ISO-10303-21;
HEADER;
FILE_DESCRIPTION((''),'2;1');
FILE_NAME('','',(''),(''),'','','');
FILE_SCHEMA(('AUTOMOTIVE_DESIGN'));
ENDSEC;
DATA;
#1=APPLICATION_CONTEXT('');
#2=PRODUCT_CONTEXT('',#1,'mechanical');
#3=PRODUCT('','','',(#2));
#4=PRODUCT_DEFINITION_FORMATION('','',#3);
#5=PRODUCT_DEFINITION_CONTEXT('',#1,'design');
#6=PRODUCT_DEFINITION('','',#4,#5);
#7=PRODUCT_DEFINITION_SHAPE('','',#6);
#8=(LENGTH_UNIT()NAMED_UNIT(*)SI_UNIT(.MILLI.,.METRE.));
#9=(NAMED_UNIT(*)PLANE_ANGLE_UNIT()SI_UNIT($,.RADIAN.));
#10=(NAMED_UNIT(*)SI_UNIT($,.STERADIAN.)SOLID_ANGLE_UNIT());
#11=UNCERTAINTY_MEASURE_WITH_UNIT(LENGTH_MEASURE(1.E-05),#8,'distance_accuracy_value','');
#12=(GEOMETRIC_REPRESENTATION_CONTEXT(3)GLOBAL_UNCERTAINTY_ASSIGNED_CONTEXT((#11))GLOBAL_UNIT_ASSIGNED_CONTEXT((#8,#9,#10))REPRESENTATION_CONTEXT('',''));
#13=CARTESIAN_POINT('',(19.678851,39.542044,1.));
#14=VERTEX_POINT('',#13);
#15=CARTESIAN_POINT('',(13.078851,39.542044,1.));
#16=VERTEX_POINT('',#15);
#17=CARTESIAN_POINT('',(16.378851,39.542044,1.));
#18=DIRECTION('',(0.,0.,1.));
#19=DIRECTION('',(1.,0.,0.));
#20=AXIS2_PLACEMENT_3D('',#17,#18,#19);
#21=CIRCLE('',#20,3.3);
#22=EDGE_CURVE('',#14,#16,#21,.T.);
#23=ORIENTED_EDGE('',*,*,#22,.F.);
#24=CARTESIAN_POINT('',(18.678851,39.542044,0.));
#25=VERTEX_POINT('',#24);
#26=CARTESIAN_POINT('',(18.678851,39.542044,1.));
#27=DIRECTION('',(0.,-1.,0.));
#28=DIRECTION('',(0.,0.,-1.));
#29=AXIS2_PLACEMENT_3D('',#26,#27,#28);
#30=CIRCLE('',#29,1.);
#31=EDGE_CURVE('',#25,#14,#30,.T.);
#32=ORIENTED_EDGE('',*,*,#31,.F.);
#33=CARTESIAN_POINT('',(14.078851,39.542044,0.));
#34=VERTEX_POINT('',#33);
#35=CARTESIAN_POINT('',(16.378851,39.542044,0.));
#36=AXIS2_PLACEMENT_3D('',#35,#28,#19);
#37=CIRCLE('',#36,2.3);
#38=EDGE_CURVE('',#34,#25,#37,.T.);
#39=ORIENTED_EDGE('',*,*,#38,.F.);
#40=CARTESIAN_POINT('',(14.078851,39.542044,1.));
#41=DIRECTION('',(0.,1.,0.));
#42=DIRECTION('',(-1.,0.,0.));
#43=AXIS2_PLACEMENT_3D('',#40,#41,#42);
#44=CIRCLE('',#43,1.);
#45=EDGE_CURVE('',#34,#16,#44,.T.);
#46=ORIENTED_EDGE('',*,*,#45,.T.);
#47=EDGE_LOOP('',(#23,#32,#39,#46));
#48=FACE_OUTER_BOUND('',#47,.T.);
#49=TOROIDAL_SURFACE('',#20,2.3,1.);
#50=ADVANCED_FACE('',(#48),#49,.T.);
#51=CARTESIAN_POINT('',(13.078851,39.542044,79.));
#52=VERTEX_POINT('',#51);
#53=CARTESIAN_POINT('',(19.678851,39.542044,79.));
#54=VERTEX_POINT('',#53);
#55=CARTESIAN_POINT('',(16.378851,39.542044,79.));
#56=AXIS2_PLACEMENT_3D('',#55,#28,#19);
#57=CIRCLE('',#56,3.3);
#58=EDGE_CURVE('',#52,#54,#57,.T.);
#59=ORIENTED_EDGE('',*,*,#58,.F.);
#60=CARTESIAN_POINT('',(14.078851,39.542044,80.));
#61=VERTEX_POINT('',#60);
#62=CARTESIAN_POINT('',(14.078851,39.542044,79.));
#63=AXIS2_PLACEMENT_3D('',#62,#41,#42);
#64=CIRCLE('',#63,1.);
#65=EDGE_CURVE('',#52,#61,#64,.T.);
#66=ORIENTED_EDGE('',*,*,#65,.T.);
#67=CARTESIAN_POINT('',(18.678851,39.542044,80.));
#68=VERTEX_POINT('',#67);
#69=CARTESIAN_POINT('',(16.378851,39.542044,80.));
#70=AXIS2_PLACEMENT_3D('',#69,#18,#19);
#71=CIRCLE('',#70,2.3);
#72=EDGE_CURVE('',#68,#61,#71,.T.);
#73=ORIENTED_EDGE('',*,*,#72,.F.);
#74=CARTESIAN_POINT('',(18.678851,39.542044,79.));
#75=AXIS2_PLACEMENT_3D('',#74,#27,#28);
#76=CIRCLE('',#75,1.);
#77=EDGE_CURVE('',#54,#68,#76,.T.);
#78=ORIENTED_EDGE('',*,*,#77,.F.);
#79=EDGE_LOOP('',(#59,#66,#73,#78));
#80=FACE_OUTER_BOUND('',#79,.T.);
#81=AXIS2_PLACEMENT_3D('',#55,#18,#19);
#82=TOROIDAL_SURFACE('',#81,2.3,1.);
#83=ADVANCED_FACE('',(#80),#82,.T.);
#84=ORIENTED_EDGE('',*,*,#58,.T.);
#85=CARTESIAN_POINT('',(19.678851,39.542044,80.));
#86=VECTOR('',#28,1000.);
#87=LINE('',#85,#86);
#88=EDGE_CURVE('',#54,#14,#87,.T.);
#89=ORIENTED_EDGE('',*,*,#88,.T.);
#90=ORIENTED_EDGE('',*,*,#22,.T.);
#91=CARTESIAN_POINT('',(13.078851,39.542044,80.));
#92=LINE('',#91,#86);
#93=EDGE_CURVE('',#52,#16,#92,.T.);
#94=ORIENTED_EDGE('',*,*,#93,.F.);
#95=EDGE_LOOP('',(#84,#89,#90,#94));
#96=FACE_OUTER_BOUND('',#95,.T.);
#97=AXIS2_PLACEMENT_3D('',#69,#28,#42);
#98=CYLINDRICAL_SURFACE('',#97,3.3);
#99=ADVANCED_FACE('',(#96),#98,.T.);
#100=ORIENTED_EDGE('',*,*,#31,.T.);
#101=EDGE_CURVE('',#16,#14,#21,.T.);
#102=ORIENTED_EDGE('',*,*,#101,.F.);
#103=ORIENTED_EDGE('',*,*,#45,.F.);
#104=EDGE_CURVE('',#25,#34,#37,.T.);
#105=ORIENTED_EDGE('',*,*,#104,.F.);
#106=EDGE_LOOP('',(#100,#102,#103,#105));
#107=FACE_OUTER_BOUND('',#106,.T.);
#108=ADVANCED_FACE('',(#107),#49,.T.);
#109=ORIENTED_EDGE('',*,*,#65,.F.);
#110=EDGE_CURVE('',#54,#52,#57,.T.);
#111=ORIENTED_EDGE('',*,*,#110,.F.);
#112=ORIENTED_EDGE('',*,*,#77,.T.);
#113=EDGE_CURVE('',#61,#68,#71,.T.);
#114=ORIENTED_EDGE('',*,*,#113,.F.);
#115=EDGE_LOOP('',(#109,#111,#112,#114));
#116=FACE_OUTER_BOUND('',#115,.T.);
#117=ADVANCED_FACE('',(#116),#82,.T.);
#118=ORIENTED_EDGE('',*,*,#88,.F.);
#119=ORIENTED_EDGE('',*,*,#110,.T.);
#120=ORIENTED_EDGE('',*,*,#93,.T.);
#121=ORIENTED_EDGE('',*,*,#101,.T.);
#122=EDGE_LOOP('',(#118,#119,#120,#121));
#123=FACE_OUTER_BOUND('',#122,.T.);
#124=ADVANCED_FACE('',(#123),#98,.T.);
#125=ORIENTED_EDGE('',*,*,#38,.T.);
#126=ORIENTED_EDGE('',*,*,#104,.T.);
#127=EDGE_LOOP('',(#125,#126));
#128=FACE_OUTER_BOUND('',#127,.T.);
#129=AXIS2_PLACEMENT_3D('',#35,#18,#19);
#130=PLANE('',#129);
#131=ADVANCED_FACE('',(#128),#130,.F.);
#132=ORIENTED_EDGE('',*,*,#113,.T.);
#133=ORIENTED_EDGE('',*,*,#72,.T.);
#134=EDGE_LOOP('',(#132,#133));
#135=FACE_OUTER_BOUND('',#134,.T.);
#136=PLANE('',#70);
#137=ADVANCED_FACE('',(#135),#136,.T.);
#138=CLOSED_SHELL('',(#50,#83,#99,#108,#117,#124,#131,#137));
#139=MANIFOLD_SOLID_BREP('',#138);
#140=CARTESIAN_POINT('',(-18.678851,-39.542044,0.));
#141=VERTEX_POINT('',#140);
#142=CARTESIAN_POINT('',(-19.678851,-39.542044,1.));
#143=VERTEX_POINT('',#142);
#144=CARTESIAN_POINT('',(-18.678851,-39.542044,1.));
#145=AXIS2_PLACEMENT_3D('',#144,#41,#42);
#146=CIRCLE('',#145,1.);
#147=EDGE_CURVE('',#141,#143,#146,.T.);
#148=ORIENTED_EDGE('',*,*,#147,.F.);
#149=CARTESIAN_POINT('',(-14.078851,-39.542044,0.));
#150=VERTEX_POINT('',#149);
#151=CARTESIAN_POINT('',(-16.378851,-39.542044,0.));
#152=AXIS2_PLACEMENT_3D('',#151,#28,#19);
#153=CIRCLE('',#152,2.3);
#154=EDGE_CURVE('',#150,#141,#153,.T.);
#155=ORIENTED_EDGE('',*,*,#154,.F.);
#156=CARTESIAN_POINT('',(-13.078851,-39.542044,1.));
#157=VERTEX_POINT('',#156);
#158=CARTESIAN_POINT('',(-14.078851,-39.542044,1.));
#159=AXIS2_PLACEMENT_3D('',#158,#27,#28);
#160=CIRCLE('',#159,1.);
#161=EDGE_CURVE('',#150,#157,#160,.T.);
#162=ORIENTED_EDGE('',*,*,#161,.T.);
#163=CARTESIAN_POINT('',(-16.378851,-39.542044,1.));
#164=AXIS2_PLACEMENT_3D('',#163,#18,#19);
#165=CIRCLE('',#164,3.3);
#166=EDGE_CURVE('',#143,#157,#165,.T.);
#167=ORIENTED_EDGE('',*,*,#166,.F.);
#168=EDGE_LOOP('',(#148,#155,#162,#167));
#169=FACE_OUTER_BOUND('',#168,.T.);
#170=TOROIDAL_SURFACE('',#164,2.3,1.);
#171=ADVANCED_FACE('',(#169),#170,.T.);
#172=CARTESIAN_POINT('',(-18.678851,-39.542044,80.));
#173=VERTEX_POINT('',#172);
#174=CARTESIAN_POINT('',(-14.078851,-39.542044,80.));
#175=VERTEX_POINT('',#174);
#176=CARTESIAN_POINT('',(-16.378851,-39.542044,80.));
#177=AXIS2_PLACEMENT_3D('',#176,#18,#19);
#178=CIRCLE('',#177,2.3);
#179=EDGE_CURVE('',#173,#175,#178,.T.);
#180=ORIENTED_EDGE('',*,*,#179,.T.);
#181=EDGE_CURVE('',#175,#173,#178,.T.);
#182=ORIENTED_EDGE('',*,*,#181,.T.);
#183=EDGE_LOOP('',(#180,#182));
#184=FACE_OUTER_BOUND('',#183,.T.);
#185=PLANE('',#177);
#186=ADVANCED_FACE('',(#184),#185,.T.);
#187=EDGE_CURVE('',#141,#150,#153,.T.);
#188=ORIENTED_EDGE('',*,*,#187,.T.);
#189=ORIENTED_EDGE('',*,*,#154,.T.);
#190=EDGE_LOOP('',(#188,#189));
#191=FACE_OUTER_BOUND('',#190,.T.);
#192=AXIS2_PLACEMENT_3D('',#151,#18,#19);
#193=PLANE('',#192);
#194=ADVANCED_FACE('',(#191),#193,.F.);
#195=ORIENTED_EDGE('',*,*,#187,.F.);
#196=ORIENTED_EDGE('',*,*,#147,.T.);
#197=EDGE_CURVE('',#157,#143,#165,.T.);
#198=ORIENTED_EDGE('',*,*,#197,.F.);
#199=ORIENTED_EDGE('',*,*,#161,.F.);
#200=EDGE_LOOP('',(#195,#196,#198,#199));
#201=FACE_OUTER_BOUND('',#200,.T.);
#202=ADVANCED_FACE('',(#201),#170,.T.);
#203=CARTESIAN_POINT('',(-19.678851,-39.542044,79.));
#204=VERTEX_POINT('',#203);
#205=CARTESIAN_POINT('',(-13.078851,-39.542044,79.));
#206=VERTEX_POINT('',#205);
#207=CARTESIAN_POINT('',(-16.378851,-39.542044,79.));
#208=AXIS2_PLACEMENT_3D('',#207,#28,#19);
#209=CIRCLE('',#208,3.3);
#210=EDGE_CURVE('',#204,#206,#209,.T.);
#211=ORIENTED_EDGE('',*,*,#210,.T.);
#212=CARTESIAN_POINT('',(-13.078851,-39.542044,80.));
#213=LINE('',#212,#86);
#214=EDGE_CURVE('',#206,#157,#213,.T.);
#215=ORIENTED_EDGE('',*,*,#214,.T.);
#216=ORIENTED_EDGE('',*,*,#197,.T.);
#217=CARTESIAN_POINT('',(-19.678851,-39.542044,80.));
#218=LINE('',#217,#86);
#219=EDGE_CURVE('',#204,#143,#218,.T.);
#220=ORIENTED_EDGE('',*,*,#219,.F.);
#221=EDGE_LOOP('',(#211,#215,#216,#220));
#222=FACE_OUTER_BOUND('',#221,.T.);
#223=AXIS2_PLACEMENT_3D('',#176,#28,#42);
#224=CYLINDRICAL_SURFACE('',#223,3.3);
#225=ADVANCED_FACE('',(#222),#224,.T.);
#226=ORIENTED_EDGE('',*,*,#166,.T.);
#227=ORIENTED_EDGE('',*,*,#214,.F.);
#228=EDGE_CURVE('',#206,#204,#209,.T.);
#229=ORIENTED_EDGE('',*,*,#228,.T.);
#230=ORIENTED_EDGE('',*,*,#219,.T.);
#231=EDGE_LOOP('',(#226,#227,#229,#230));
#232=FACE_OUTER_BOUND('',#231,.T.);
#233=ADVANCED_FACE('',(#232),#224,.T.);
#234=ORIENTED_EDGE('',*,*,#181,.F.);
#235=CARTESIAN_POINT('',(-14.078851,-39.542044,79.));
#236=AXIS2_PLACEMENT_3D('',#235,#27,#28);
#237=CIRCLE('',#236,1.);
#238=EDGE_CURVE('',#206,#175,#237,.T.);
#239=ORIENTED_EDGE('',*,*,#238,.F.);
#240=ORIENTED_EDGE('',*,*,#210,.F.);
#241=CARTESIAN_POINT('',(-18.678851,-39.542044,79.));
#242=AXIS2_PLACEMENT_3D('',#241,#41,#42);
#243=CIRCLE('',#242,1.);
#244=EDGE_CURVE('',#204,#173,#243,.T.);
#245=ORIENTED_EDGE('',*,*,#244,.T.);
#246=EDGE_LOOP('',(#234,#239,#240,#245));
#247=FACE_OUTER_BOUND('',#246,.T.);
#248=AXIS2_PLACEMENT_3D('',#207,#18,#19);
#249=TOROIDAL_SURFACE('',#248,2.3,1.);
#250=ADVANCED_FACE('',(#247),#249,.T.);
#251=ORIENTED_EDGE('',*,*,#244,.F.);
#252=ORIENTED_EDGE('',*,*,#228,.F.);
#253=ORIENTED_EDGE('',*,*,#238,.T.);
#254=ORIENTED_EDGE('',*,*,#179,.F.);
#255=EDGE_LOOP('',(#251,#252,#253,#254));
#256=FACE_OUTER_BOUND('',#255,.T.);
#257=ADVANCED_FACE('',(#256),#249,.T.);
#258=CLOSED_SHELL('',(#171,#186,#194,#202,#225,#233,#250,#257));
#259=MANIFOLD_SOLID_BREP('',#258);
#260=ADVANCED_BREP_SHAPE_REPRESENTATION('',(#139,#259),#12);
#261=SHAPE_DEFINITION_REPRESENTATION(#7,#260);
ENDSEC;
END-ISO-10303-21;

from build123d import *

# Parameters (mm, degrees)
SKETCH1_R             = 3.3
BOSS_EXTRUDE1_DEPTH   = 80
BOSS_EXTRUDE1_2_DEPTH = 80
FILLET1_R             = 1
FILLET2_R             = 1


with BuildPart() as part:
    # Sketch1 → Boss-Extrude1 (new body)
    with BuildSketch(Plane.XY):
        with Locations((-16.378850905, -39.542043991)):
            Circle(SKETCH1_R)
    extrude(amount=BOSS_EXTRUDE1_DEPTH)

    # Fillet1
    fillet1_edges = [part.edges().sort_by_distance(p)[0] for p in [
        (-19.678850905, -39.542043991, 0),
        (-19.678850905, -39.542043991, 80),
    ]]
    fillet(fillet1_edges, radius=FILLET1_R)


with BuildPart() as body_2:
    # Sketch1 → Boss-Extrude1 2 (new body)
    with BuildSketch(Plane.XY):
        with Locations((16.378850905, 39.542043991)):
            Circle(SKETCH1_R)
    extrude(amount=BOSS_EXTRUDE1_2_DEPTH)

    # Fillet2
    fillet2_edges = [body_2.edges().sort_by_distance(p)[0] for p in [
        (13.078850905, 39.542043991, 0),
        (13.078850905, 39.542043991, 80),
    ]]
    fillet(fillet2_edges, radius=FILLET2_R)


solid = Compound([part.part, body_2.part])
